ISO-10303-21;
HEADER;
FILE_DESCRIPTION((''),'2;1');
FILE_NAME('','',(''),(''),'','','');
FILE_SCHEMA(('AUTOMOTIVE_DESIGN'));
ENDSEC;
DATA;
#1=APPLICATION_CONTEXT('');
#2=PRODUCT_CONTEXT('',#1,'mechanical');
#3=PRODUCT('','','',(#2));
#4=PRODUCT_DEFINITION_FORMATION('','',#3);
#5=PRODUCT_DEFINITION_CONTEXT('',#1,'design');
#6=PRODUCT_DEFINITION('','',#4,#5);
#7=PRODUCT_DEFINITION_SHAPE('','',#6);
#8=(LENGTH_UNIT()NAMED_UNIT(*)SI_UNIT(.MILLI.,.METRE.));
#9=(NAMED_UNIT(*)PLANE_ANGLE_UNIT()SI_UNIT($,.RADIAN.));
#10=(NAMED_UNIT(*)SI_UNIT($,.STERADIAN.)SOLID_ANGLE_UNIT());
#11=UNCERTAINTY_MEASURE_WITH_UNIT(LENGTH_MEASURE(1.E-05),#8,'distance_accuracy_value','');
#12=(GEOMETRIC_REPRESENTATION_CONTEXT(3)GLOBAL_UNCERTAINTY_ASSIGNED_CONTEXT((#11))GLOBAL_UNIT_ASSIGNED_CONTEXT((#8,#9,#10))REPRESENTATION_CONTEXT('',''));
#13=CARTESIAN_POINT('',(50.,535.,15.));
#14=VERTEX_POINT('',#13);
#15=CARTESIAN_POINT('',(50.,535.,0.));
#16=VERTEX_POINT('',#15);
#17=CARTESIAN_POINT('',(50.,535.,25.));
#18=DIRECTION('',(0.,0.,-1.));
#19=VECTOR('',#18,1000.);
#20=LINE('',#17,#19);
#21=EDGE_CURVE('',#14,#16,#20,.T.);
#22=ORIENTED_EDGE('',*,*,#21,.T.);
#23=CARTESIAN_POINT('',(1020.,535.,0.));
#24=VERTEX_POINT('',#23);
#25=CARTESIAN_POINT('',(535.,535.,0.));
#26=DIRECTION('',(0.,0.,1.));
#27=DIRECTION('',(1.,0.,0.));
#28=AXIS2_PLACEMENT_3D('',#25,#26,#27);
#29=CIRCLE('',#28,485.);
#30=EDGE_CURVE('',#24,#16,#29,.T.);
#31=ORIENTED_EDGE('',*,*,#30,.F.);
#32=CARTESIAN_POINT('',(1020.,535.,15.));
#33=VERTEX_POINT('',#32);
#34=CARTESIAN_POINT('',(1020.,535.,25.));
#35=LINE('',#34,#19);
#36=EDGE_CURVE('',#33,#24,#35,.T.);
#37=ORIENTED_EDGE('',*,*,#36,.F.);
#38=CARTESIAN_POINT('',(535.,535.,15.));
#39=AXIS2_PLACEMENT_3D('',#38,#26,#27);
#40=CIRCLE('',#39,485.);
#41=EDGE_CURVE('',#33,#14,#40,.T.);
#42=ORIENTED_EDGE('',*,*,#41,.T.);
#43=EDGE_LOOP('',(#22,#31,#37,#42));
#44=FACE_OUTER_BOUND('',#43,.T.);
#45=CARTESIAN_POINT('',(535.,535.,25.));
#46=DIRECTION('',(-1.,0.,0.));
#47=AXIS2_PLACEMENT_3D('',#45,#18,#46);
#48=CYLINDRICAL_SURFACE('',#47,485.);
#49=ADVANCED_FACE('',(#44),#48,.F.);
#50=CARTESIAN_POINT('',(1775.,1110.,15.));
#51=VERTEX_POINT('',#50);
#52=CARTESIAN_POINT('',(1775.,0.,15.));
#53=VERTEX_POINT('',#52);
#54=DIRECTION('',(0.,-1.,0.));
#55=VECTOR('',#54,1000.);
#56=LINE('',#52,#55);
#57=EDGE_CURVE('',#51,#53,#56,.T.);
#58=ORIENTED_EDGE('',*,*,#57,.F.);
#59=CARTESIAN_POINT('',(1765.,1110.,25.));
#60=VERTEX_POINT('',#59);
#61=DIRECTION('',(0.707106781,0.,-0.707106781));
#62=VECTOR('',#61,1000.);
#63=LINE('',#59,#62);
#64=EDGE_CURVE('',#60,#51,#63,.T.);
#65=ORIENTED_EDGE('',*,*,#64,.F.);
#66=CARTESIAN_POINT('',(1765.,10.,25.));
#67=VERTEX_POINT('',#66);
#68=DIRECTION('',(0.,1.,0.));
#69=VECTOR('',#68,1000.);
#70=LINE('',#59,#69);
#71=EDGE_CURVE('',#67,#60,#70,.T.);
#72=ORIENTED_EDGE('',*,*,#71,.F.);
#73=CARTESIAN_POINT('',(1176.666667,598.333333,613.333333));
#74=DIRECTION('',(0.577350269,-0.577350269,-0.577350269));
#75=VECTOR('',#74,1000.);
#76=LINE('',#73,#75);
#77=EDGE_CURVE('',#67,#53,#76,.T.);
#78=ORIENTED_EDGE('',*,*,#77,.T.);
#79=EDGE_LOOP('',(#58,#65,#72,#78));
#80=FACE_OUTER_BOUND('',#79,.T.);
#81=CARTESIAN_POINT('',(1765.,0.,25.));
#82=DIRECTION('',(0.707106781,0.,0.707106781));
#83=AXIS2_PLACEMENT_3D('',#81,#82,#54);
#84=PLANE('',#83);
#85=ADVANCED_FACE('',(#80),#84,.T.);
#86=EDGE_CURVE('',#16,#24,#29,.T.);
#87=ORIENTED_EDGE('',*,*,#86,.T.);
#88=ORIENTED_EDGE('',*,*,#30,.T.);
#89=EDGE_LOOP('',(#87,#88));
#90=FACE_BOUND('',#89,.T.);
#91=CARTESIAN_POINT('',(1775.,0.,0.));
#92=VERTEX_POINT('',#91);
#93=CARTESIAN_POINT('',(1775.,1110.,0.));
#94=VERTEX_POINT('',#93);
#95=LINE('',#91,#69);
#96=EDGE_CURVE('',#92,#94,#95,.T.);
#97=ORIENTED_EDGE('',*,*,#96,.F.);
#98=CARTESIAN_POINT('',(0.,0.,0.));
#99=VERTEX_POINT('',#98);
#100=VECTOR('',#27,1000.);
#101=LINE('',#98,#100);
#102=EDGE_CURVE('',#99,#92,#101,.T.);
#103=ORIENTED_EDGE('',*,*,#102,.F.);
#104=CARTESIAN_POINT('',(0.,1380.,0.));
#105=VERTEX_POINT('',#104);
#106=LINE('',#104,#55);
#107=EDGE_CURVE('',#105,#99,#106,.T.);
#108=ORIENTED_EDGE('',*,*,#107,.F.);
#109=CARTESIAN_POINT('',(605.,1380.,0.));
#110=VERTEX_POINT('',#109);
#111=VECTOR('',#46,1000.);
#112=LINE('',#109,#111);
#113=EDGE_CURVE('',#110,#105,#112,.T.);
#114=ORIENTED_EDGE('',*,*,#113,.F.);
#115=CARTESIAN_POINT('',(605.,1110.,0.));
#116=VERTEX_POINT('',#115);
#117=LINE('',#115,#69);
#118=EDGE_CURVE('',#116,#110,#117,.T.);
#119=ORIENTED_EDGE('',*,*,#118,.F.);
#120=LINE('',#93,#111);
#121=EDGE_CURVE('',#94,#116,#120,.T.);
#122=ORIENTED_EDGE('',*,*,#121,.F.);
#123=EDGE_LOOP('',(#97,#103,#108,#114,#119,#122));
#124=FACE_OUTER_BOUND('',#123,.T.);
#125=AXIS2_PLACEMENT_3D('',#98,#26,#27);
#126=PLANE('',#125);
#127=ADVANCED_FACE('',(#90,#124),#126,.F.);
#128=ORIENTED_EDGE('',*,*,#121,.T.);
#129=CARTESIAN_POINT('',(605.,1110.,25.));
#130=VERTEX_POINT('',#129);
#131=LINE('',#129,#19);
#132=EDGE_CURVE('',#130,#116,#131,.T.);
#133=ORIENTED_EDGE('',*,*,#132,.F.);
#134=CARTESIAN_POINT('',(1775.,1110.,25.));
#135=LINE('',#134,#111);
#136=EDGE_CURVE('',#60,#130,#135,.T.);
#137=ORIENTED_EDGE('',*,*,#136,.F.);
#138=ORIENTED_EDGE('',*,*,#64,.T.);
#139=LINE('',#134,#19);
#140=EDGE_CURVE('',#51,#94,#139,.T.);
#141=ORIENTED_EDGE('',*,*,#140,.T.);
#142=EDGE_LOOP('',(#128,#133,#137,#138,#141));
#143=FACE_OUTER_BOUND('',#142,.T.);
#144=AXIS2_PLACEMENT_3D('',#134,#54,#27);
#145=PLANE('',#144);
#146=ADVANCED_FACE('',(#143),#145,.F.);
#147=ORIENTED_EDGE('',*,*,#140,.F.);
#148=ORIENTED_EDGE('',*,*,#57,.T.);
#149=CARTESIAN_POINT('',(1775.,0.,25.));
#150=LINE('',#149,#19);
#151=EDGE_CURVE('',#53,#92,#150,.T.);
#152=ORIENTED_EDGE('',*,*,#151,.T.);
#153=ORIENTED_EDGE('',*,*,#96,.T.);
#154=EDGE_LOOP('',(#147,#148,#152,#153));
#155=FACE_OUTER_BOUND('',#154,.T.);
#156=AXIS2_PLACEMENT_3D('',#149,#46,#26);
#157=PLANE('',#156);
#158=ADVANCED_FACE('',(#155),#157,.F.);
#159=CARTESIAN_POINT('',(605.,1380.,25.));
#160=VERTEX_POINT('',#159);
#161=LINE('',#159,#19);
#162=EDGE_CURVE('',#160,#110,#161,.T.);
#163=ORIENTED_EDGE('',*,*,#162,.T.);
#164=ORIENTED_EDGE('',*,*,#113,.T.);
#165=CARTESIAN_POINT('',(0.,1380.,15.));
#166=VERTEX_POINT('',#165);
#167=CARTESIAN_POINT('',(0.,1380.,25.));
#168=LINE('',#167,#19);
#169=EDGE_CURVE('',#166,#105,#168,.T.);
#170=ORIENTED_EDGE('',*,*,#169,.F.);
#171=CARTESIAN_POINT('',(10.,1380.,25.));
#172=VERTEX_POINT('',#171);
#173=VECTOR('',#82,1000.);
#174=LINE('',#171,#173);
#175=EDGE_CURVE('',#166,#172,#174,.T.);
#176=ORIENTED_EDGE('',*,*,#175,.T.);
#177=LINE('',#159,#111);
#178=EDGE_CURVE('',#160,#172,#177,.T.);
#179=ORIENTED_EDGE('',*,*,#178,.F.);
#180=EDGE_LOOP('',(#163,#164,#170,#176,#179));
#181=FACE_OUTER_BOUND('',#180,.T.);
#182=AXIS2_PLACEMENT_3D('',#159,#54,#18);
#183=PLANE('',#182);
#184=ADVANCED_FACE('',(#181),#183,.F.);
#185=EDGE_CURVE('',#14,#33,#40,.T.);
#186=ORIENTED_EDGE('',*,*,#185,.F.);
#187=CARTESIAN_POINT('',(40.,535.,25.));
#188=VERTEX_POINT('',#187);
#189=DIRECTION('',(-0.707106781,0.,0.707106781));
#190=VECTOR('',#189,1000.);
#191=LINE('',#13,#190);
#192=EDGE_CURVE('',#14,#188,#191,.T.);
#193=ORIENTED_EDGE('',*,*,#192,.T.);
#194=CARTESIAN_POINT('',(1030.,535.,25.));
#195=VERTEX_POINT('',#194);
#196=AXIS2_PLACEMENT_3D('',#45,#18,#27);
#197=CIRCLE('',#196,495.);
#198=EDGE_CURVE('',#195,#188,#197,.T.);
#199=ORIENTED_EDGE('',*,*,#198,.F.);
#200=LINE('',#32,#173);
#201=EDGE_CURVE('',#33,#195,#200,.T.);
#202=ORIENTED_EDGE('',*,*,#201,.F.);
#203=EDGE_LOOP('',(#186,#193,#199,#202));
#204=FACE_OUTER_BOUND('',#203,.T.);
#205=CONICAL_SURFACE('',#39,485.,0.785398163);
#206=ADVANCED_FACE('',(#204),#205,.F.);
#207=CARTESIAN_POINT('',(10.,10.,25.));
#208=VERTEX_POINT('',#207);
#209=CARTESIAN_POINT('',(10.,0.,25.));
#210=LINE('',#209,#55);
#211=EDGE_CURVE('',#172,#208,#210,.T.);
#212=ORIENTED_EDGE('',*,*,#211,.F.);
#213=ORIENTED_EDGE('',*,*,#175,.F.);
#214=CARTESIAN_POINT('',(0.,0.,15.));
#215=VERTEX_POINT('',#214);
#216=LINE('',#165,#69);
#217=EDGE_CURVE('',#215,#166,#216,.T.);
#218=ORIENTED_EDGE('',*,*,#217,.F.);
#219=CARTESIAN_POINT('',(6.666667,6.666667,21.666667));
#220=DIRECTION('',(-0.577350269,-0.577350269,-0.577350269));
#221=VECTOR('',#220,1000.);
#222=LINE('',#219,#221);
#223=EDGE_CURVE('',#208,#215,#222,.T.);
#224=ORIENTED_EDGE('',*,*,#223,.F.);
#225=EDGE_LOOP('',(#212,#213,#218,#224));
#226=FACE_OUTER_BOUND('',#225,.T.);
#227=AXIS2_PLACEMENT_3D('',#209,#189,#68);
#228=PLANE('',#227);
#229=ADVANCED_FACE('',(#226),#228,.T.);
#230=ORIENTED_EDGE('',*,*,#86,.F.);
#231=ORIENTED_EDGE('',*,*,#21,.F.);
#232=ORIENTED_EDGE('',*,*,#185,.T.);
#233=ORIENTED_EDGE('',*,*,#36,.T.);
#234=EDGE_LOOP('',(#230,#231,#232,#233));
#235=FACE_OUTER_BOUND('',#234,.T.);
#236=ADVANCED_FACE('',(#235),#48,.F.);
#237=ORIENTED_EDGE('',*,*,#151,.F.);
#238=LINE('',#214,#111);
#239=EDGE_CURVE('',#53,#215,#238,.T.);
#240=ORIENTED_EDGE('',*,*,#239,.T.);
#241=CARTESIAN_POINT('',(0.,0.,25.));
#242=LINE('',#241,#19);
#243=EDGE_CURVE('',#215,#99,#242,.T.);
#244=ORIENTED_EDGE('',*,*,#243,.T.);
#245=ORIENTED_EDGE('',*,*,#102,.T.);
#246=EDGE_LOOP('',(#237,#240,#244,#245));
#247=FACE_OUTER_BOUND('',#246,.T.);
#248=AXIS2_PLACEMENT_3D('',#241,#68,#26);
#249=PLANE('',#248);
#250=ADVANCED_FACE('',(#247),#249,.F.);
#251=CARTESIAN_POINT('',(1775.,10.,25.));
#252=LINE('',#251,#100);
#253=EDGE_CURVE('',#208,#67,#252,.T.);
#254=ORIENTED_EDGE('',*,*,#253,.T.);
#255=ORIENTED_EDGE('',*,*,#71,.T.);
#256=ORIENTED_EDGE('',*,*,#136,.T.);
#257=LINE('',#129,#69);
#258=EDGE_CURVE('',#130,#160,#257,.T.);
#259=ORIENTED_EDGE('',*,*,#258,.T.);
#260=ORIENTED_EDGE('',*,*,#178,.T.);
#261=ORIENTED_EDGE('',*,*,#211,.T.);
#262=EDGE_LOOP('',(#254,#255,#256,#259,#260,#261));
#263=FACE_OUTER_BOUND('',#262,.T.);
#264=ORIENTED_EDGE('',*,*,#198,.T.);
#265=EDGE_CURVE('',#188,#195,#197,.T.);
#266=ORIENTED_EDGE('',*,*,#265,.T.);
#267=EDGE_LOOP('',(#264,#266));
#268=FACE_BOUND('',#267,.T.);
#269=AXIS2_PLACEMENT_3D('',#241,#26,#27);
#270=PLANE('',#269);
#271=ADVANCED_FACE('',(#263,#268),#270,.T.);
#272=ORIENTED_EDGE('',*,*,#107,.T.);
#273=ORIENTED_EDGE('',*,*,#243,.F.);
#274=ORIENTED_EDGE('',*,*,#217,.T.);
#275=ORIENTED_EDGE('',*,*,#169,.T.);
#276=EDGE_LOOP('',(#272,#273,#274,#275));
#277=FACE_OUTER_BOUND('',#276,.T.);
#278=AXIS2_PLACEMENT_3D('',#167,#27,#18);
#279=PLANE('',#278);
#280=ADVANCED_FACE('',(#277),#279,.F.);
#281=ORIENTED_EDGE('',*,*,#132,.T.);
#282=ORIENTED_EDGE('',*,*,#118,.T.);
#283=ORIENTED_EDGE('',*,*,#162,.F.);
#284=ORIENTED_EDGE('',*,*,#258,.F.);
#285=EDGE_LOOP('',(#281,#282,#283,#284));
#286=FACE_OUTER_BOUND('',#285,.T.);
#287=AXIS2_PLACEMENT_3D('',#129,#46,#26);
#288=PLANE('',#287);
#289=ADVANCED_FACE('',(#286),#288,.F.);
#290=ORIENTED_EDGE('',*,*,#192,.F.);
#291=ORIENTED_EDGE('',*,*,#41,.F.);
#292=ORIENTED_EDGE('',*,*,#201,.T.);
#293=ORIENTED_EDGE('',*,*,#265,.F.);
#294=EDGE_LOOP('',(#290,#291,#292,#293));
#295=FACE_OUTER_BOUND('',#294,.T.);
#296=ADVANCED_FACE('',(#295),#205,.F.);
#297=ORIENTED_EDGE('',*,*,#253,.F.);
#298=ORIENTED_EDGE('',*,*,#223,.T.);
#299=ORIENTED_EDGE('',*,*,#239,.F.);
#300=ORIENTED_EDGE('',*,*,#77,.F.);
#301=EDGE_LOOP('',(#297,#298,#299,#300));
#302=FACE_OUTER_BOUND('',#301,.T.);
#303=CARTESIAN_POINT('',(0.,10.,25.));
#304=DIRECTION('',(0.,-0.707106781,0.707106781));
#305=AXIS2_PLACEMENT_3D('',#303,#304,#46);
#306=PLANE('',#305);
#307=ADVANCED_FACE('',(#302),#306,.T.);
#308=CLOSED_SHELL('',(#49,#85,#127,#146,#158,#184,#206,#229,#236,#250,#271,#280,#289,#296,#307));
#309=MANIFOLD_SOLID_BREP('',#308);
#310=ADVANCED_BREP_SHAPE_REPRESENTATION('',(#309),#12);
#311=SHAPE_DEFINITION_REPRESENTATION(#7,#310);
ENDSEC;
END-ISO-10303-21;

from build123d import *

# Parameters (mm, degrees)
SKETCH1_R           = 485
BOSS_EXTRUDE1_DEPTH = 25
CHAMFER1_SIZE       = 10


with BuildPart() as part:
    # Sketch1 → Boss-Extrude1 (new body)
    with BuildSketch(Plane.XY):
        Polygon((0, 0), (1775, 0), (1775, 1110), (605, 1110), (605, 1380), (0, 1380), align=None)
        with Locations((535, 535)):
            Circle(SKETCH1_R, mode=Mode.SUBTRACT)
    extrude(amount=BOSS_EXTRUDE1_DEPTH)

    # Chamfer1
    chamfer1_edges = [part.edges().sort_by_distance(p)[0] for p in [
        (1775, 555, 25),
        (50, 535, 25),
        (0, 690, 25),
        (887.5, 0, 25),
    ]]
    chamfer(chamfer1_edges, length=CHAMFER1_SIZE)


solid = part.part
